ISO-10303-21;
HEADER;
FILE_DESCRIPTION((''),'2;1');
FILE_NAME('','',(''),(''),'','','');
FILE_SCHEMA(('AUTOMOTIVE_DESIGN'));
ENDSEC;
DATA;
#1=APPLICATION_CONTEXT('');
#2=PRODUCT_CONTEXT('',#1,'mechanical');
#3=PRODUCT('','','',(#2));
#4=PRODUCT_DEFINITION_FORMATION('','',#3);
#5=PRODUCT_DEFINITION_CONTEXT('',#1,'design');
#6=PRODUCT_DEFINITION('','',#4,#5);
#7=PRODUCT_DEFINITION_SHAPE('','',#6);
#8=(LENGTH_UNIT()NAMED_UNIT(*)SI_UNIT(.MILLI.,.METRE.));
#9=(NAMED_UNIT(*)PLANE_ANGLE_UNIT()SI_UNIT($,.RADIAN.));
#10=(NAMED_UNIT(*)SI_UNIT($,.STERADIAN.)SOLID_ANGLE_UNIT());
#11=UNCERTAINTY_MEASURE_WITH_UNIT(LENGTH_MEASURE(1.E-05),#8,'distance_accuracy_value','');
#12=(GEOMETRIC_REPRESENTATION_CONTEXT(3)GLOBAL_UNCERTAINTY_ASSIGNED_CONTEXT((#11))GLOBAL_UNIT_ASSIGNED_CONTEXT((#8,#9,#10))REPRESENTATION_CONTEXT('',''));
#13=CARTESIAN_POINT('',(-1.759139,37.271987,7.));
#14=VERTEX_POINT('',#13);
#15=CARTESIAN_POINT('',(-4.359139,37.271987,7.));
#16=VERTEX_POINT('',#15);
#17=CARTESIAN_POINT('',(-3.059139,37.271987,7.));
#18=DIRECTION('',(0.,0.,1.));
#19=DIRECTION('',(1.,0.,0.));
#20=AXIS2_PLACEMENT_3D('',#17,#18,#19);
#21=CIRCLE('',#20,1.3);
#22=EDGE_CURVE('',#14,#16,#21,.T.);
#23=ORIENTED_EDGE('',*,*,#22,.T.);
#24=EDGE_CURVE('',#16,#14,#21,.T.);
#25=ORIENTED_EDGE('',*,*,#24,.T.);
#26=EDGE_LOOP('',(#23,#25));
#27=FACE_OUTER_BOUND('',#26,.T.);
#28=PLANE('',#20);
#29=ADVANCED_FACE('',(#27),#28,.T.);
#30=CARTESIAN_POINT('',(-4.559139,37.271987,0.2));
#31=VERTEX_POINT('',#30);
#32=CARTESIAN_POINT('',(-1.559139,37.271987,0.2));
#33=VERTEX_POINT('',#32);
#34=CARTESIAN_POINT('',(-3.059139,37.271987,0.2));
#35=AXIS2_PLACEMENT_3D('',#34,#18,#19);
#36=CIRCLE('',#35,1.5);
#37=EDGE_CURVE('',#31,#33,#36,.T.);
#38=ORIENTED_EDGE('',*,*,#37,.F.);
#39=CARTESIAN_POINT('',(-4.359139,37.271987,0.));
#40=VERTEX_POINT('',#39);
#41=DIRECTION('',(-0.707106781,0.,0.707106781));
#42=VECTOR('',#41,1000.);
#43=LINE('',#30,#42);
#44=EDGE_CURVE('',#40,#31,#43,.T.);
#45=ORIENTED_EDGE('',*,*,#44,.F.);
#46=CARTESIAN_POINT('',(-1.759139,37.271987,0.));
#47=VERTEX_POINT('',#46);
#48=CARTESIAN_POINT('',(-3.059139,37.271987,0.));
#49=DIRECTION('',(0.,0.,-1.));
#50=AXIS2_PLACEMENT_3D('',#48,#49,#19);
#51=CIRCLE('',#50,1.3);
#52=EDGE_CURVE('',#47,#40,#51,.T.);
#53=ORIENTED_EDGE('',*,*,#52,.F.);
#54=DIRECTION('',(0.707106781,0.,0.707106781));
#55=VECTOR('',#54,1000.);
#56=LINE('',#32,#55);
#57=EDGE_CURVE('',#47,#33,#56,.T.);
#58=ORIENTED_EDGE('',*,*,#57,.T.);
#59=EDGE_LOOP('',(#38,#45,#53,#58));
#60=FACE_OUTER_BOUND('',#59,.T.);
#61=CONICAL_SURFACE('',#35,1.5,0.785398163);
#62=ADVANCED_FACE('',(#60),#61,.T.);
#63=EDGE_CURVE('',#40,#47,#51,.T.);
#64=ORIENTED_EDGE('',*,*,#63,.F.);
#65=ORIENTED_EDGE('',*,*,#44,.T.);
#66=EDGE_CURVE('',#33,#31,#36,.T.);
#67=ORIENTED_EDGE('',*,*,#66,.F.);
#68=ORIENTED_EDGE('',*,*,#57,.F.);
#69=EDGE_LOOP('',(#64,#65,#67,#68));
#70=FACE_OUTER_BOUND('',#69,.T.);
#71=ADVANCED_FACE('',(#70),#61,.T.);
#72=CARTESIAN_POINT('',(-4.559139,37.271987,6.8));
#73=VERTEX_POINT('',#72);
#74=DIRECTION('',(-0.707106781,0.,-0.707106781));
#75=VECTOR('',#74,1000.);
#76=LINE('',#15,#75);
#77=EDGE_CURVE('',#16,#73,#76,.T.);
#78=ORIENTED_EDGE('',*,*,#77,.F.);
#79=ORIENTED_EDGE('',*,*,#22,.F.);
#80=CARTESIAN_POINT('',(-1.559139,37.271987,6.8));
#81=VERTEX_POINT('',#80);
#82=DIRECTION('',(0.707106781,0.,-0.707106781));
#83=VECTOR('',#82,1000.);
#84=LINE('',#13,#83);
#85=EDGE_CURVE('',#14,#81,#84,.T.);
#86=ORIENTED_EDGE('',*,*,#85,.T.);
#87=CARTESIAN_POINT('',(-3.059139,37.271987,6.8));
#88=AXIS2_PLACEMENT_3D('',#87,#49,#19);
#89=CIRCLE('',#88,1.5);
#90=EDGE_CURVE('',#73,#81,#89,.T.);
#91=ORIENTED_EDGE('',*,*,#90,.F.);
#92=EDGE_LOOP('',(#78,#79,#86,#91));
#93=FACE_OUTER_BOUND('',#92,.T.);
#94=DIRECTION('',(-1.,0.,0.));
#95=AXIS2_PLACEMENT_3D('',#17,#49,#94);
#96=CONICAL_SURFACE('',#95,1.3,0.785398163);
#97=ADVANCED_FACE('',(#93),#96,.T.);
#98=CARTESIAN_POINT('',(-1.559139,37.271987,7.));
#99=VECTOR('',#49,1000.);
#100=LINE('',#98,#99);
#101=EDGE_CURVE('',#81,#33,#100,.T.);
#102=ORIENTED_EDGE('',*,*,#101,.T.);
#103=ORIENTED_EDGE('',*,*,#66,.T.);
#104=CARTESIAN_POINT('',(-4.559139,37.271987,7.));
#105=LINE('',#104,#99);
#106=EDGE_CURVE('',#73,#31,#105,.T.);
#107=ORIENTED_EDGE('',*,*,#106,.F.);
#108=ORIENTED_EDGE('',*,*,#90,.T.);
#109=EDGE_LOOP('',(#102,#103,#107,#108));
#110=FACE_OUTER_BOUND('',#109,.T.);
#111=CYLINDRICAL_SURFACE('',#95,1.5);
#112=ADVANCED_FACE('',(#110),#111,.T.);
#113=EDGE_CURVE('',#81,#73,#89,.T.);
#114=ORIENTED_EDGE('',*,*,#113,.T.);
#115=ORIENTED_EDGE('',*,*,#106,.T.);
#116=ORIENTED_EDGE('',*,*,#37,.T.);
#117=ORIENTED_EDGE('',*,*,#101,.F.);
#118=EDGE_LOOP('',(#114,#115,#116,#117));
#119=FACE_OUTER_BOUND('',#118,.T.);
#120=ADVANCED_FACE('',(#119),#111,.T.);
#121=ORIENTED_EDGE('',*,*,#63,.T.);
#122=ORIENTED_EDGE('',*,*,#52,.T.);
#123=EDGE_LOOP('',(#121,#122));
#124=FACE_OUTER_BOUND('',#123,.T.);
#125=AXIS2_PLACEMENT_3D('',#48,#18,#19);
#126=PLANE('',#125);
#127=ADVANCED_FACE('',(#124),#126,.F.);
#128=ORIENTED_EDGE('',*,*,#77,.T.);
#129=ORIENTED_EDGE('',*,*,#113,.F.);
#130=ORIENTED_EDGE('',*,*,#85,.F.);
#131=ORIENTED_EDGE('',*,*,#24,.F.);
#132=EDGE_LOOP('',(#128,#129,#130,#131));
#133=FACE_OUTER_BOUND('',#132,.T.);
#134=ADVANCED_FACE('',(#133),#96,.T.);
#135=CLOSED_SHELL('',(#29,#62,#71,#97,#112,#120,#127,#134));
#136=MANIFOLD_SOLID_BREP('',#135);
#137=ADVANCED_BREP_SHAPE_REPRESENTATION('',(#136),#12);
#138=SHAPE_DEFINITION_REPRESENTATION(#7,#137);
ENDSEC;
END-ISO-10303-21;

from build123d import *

# Parameters (mm, degrees)
SKETCH2_R           = 1.5
BOSS_EXTRUDE2_DEPTH = 7
CHAMFER1_SIZE       = 0.2


with BuildPart() as part:
    # Sketch2 → Boss-Extrude2 (new body)
    with BuildSketch(Plane.XY):
        with Locations((-3.05913896, 37.271986881)):
            Circle(SKETCH2_R)
    extrude(amount=BOSS_EXTRUDE2_DEPTH)

    # Chamfer1
    chamfer1_edges = [part.edges().sort_by_distance(p)[0] for p in [
        (-4.55913896, 37.271986881, 0),
        (-4.55913896, 37.271986881, 7),
    ]]
    chamfer(chamfer1_edges, length=CHAMFER1_SIZE)


solid = part.part
